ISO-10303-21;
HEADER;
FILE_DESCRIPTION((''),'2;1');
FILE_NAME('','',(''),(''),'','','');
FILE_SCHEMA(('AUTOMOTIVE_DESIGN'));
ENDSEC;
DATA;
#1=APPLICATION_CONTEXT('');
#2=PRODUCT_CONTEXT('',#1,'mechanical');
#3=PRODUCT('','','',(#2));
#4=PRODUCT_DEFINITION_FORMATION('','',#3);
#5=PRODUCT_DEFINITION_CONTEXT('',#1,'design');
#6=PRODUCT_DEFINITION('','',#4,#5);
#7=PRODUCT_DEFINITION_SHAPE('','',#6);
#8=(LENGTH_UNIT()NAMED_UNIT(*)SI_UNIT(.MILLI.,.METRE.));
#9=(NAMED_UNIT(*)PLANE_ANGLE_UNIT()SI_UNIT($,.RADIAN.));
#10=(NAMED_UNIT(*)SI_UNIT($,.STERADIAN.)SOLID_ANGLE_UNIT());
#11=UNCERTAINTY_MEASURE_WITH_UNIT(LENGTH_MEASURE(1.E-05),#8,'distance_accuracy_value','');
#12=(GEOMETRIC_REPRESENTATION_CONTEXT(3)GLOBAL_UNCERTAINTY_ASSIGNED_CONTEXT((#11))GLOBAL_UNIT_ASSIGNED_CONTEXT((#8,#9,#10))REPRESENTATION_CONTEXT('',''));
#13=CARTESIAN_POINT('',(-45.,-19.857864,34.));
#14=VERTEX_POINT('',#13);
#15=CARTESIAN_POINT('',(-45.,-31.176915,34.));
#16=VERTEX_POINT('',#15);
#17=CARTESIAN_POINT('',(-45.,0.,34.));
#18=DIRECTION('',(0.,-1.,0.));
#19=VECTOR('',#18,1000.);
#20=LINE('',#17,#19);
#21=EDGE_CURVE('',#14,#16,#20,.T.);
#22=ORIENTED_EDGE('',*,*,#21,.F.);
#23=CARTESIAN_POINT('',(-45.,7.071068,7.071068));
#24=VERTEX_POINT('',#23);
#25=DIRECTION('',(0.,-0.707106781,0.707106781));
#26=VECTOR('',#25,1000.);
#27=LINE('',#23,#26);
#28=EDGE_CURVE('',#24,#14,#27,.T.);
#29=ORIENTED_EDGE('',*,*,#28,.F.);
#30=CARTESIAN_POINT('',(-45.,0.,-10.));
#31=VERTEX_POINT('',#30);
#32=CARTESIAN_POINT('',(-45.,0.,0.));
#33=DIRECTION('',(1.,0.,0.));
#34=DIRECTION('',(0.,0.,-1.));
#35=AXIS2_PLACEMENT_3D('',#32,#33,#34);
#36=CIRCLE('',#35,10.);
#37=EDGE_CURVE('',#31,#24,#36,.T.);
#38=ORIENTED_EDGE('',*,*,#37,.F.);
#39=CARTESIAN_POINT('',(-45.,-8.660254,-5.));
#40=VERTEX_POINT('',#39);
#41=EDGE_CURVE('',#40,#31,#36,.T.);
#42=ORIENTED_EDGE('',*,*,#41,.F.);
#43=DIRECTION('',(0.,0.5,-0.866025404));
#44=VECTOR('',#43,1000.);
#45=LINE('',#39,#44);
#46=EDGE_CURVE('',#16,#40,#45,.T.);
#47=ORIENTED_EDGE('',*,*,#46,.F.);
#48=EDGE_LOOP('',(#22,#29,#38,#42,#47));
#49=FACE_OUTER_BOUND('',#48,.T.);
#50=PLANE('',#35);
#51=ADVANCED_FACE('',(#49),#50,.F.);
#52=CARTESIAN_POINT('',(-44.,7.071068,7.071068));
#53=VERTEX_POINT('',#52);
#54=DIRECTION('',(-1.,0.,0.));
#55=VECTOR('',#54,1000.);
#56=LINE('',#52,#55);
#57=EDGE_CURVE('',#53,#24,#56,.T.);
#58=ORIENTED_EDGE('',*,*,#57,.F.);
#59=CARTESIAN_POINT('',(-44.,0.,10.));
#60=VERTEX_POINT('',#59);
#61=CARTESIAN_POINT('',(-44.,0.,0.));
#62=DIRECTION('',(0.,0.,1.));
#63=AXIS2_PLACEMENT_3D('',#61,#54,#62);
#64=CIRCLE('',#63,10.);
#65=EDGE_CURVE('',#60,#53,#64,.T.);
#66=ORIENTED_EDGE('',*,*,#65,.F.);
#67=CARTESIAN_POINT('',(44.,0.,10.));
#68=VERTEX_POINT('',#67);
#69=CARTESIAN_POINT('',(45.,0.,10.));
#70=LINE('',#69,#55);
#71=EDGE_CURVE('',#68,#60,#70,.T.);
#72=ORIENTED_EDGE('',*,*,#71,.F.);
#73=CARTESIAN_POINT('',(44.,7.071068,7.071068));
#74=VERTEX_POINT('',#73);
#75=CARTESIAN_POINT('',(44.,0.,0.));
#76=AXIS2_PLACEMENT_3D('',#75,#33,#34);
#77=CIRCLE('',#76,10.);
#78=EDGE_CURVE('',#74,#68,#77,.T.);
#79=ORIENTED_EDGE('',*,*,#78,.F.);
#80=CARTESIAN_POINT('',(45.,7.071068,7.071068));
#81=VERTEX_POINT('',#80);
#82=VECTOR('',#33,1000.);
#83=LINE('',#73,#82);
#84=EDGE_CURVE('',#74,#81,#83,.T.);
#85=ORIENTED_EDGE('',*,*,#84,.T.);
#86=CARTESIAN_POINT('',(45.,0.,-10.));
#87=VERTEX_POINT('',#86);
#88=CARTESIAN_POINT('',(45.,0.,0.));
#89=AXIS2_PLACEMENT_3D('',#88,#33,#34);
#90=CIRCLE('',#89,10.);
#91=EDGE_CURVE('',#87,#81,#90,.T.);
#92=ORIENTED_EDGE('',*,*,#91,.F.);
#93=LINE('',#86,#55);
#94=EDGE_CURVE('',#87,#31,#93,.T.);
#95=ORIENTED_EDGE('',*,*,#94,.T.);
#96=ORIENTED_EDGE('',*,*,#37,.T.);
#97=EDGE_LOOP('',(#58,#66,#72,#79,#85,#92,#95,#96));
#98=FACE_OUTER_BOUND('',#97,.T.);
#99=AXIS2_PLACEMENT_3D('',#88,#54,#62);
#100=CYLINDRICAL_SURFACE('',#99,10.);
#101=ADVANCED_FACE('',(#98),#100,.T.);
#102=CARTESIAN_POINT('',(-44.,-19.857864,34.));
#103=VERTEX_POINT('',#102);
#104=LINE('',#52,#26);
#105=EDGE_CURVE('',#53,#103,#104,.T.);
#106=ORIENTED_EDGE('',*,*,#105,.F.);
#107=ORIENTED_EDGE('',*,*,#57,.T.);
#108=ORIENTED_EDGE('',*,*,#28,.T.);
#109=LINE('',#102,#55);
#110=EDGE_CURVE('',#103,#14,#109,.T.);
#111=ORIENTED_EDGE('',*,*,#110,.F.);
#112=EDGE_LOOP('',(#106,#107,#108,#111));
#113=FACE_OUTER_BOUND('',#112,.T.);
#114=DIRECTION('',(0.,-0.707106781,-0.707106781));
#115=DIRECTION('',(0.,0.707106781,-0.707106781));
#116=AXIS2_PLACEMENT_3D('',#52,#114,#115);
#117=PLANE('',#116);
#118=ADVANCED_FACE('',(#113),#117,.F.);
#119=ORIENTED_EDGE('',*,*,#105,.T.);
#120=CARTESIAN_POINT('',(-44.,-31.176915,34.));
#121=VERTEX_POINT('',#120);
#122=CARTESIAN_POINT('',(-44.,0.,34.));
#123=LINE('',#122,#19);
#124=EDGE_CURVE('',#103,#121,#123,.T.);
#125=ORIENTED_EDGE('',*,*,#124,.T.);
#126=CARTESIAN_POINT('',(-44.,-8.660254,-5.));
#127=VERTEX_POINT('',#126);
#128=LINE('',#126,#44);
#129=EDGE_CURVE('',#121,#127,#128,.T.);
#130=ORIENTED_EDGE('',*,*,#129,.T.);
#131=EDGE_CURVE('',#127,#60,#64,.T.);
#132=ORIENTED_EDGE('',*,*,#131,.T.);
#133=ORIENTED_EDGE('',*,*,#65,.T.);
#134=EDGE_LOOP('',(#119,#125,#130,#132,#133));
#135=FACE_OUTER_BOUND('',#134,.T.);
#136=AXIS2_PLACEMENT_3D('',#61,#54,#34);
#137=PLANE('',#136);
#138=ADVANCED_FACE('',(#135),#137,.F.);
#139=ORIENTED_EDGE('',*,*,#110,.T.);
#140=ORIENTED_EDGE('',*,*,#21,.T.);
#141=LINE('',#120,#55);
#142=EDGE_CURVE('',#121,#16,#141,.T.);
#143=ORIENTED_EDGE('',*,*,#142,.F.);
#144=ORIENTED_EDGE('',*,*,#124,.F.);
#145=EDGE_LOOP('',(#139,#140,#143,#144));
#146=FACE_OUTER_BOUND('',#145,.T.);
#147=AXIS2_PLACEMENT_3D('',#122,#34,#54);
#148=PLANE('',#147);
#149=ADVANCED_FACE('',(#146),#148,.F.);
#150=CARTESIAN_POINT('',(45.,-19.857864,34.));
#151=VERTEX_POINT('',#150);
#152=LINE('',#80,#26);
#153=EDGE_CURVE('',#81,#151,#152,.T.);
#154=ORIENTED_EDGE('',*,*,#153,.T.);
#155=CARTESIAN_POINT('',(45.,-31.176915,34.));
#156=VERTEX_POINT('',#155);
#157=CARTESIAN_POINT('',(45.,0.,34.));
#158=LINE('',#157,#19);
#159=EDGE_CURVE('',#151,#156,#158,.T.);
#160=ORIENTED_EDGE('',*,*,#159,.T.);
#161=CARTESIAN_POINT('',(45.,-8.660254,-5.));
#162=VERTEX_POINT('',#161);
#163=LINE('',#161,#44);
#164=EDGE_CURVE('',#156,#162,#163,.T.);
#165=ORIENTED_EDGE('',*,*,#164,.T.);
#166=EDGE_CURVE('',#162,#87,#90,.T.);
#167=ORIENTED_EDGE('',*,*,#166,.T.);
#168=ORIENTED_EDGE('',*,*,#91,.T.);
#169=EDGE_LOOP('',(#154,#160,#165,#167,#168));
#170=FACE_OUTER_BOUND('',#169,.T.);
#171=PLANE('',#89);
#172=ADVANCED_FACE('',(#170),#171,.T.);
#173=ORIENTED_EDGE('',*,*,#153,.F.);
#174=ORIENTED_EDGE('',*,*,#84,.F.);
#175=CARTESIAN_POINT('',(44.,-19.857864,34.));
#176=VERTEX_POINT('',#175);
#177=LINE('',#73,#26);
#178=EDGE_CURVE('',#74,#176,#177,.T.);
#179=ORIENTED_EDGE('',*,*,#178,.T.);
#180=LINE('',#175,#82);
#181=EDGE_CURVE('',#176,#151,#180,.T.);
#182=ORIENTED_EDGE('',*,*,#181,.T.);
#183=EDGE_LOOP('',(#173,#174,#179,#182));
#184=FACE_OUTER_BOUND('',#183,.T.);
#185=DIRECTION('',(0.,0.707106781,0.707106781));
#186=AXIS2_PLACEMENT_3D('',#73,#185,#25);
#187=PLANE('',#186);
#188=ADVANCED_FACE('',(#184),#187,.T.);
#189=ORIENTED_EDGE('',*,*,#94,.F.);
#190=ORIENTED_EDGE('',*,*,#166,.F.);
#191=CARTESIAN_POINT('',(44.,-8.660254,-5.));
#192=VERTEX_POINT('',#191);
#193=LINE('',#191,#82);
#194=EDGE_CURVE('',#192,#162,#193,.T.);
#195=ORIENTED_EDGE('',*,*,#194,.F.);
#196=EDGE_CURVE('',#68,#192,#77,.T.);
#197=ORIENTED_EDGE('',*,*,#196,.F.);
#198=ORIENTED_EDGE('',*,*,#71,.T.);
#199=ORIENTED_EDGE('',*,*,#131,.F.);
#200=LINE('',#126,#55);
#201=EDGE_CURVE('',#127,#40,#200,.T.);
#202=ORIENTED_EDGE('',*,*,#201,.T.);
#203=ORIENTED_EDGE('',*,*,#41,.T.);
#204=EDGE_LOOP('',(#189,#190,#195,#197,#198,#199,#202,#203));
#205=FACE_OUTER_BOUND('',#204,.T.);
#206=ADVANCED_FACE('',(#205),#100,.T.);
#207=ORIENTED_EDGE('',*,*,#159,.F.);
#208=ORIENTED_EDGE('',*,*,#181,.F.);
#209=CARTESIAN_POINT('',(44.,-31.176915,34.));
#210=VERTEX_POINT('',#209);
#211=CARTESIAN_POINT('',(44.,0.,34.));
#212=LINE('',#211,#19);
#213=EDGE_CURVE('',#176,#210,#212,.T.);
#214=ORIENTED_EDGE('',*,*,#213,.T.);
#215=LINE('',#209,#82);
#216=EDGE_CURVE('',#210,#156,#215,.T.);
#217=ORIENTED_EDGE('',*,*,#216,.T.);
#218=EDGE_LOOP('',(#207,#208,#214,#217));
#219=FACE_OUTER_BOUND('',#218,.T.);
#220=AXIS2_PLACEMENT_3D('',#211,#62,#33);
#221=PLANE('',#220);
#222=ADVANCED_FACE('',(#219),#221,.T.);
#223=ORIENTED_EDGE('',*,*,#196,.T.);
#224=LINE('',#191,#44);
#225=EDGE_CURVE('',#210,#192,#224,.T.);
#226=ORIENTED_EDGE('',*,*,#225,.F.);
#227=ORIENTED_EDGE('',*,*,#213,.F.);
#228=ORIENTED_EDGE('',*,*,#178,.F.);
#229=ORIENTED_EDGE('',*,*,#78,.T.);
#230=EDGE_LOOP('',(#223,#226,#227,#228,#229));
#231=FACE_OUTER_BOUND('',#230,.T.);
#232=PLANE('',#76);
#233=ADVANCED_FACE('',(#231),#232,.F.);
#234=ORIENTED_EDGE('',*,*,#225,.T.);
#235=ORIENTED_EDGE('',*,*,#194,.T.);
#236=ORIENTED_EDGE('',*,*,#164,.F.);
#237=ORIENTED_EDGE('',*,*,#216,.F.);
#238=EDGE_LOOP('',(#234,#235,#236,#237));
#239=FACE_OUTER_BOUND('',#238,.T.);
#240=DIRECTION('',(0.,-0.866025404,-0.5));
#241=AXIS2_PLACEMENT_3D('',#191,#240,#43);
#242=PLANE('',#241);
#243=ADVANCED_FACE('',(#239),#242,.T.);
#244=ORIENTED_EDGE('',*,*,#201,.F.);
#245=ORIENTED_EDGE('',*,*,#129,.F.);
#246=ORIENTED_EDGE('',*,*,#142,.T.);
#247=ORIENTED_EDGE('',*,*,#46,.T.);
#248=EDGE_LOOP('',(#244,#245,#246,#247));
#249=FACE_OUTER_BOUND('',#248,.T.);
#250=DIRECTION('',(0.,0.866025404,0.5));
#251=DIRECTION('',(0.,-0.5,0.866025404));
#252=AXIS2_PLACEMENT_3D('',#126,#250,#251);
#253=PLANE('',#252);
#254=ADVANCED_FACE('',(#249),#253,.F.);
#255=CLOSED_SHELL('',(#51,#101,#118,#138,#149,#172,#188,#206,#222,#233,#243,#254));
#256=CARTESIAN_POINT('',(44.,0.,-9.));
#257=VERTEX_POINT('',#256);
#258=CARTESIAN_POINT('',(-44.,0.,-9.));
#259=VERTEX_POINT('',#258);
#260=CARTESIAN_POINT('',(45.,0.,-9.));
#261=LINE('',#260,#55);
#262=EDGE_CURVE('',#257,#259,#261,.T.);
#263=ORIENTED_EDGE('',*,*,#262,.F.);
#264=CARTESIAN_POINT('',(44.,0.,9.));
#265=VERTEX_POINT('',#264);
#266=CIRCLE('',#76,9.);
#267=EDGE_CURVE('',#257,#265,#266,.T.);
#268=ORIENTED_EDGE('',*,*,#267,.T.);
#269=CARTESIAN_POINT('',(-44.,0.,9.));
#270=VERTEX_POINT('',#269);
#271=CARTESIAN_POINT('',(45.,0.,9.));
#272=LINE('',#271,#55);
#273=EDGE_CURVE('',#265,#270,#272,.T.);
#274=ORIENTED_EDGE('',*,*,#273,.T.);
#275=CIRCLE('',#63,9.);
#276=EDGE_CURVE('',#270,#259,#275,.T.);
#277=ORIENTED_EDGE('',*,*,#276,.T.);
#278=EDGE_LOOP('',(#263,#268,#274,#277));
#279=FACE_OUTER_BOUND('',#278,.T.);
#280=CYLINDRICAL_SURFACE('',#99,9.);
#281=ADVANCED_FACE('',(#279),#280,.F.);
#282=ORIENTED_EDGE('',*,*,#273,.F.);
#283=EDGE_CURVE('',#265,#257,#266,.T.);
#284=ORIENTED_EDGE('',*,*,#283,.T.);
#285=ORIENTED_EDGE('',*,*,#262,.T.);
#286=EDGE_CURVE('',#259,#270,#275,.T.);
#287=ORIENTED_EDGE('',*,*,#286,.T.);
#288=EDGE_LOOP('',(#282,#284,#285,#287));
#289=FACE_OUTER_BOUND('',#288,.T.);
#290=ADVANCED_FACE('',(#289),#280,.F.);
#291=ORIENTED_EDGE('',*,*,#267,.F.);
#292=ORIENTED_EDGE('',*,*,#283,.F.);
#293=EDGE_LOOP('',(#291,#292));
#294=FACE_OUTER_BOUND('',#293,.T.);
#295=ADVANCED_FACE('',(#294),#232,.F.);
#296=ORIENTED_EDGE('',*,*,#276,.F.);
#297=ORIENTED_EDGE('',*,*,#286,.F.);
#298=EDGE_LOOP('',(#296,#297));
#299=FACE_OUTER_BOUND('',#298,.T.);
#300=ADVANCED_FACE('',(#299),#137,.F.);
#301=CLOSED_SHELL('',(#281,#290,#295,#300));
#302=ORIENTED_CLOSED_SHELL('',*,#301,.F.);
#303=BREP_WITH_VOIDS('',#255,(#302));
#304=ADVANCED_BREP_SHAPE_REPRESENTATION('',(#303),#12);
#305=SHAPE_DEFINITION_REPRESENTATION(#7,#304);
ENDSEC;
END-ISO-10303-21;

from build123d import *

# Parameters (mm, degrees)
SKETCH1_R           = 10
SKETCH1_R_2         = 9
BOSS_EXTRUDE1_DEPTH = 45
SKETCH2_R           = 10
SKETCH2_R_2         = 9
BOSS_EXTRUDE2_DEPTH = 1


with BuildPart() as part:
    # Sketch1 → Boss-Extrude1 (new, symmetric)
    with BuildSketch(Plane(origin=(0, 0, 0), x_dir=(0, 0, -1), z_dir=(1, 0, 0))):
        with Locations(Location((0, 0, 0), (0, 0, 180))):
            Circle(SKETCH1_R)
        with Locations(Location((0, 0, 0), (0, 0, 180))):
            Circle(SKETCH1_R_2, mode=Mode.SUBTRACT)
    extrude(amount=BOSS_EXTRUDE1_DEPTH, both=True)

    # Sketch2 → Boss-Extrude2 (add)
    # profile 1 of 3: a face of its own
    with BuildSketch(Plane(origin=(45, 0, 0), x_dir=(0, 0, -1), z_dir=(1, 0, 0))):
        with BuildLine():
            ThreePointArc((5, -8.660254038), (-7.933533403, -6.08761429), (-7.071067812, 7.071067812))
            Line((-7.071067812, 7.071067812), (-34, -19.857864376))
            Line((-34, -19.857864376), (-34, -31.176914536))
            Line((-34, -31.176914536), (5, -8.660254038))
        make_face()
    # profile 2 of 3: a face of its own
    with BuildSketch(Plane(origin=(45, 0, 0), x_dir=(0, 0, -1), z_dir=(1, 0, 0))):
        with Locations(Location((0, 0, 0), (0, 0, 135))):
            Circle(SKETCH2_R)
        with Locations(Location((0, 0, 0), (0, 0, 180))):
            Circle(SKETCH2_R_2, mode=Mode.SUBTRACT)
    # profile 3 of 3: a face of its own
    with BuildSketch(Plane(origin=(45, 0, 0), x_dir=(0, 0, -1), z_dir=(1, 0, 0))):
        with Locations(Location((0, 0, 0), (0, 0, 180))):
            Circle(SKETCH2_R_2)
    boss_extrude2 = extrude(amount=-BOSS_EXTRUDE2_DEPTH)

    # Mirror1: Boss-Extrude2 across plane
    add(boss_extrude2.mirror(Plane(origin=(0, 0, 0), x_dir=(0, 0, 1), z_dir=(1, 0, 0))))


solid = part.part
